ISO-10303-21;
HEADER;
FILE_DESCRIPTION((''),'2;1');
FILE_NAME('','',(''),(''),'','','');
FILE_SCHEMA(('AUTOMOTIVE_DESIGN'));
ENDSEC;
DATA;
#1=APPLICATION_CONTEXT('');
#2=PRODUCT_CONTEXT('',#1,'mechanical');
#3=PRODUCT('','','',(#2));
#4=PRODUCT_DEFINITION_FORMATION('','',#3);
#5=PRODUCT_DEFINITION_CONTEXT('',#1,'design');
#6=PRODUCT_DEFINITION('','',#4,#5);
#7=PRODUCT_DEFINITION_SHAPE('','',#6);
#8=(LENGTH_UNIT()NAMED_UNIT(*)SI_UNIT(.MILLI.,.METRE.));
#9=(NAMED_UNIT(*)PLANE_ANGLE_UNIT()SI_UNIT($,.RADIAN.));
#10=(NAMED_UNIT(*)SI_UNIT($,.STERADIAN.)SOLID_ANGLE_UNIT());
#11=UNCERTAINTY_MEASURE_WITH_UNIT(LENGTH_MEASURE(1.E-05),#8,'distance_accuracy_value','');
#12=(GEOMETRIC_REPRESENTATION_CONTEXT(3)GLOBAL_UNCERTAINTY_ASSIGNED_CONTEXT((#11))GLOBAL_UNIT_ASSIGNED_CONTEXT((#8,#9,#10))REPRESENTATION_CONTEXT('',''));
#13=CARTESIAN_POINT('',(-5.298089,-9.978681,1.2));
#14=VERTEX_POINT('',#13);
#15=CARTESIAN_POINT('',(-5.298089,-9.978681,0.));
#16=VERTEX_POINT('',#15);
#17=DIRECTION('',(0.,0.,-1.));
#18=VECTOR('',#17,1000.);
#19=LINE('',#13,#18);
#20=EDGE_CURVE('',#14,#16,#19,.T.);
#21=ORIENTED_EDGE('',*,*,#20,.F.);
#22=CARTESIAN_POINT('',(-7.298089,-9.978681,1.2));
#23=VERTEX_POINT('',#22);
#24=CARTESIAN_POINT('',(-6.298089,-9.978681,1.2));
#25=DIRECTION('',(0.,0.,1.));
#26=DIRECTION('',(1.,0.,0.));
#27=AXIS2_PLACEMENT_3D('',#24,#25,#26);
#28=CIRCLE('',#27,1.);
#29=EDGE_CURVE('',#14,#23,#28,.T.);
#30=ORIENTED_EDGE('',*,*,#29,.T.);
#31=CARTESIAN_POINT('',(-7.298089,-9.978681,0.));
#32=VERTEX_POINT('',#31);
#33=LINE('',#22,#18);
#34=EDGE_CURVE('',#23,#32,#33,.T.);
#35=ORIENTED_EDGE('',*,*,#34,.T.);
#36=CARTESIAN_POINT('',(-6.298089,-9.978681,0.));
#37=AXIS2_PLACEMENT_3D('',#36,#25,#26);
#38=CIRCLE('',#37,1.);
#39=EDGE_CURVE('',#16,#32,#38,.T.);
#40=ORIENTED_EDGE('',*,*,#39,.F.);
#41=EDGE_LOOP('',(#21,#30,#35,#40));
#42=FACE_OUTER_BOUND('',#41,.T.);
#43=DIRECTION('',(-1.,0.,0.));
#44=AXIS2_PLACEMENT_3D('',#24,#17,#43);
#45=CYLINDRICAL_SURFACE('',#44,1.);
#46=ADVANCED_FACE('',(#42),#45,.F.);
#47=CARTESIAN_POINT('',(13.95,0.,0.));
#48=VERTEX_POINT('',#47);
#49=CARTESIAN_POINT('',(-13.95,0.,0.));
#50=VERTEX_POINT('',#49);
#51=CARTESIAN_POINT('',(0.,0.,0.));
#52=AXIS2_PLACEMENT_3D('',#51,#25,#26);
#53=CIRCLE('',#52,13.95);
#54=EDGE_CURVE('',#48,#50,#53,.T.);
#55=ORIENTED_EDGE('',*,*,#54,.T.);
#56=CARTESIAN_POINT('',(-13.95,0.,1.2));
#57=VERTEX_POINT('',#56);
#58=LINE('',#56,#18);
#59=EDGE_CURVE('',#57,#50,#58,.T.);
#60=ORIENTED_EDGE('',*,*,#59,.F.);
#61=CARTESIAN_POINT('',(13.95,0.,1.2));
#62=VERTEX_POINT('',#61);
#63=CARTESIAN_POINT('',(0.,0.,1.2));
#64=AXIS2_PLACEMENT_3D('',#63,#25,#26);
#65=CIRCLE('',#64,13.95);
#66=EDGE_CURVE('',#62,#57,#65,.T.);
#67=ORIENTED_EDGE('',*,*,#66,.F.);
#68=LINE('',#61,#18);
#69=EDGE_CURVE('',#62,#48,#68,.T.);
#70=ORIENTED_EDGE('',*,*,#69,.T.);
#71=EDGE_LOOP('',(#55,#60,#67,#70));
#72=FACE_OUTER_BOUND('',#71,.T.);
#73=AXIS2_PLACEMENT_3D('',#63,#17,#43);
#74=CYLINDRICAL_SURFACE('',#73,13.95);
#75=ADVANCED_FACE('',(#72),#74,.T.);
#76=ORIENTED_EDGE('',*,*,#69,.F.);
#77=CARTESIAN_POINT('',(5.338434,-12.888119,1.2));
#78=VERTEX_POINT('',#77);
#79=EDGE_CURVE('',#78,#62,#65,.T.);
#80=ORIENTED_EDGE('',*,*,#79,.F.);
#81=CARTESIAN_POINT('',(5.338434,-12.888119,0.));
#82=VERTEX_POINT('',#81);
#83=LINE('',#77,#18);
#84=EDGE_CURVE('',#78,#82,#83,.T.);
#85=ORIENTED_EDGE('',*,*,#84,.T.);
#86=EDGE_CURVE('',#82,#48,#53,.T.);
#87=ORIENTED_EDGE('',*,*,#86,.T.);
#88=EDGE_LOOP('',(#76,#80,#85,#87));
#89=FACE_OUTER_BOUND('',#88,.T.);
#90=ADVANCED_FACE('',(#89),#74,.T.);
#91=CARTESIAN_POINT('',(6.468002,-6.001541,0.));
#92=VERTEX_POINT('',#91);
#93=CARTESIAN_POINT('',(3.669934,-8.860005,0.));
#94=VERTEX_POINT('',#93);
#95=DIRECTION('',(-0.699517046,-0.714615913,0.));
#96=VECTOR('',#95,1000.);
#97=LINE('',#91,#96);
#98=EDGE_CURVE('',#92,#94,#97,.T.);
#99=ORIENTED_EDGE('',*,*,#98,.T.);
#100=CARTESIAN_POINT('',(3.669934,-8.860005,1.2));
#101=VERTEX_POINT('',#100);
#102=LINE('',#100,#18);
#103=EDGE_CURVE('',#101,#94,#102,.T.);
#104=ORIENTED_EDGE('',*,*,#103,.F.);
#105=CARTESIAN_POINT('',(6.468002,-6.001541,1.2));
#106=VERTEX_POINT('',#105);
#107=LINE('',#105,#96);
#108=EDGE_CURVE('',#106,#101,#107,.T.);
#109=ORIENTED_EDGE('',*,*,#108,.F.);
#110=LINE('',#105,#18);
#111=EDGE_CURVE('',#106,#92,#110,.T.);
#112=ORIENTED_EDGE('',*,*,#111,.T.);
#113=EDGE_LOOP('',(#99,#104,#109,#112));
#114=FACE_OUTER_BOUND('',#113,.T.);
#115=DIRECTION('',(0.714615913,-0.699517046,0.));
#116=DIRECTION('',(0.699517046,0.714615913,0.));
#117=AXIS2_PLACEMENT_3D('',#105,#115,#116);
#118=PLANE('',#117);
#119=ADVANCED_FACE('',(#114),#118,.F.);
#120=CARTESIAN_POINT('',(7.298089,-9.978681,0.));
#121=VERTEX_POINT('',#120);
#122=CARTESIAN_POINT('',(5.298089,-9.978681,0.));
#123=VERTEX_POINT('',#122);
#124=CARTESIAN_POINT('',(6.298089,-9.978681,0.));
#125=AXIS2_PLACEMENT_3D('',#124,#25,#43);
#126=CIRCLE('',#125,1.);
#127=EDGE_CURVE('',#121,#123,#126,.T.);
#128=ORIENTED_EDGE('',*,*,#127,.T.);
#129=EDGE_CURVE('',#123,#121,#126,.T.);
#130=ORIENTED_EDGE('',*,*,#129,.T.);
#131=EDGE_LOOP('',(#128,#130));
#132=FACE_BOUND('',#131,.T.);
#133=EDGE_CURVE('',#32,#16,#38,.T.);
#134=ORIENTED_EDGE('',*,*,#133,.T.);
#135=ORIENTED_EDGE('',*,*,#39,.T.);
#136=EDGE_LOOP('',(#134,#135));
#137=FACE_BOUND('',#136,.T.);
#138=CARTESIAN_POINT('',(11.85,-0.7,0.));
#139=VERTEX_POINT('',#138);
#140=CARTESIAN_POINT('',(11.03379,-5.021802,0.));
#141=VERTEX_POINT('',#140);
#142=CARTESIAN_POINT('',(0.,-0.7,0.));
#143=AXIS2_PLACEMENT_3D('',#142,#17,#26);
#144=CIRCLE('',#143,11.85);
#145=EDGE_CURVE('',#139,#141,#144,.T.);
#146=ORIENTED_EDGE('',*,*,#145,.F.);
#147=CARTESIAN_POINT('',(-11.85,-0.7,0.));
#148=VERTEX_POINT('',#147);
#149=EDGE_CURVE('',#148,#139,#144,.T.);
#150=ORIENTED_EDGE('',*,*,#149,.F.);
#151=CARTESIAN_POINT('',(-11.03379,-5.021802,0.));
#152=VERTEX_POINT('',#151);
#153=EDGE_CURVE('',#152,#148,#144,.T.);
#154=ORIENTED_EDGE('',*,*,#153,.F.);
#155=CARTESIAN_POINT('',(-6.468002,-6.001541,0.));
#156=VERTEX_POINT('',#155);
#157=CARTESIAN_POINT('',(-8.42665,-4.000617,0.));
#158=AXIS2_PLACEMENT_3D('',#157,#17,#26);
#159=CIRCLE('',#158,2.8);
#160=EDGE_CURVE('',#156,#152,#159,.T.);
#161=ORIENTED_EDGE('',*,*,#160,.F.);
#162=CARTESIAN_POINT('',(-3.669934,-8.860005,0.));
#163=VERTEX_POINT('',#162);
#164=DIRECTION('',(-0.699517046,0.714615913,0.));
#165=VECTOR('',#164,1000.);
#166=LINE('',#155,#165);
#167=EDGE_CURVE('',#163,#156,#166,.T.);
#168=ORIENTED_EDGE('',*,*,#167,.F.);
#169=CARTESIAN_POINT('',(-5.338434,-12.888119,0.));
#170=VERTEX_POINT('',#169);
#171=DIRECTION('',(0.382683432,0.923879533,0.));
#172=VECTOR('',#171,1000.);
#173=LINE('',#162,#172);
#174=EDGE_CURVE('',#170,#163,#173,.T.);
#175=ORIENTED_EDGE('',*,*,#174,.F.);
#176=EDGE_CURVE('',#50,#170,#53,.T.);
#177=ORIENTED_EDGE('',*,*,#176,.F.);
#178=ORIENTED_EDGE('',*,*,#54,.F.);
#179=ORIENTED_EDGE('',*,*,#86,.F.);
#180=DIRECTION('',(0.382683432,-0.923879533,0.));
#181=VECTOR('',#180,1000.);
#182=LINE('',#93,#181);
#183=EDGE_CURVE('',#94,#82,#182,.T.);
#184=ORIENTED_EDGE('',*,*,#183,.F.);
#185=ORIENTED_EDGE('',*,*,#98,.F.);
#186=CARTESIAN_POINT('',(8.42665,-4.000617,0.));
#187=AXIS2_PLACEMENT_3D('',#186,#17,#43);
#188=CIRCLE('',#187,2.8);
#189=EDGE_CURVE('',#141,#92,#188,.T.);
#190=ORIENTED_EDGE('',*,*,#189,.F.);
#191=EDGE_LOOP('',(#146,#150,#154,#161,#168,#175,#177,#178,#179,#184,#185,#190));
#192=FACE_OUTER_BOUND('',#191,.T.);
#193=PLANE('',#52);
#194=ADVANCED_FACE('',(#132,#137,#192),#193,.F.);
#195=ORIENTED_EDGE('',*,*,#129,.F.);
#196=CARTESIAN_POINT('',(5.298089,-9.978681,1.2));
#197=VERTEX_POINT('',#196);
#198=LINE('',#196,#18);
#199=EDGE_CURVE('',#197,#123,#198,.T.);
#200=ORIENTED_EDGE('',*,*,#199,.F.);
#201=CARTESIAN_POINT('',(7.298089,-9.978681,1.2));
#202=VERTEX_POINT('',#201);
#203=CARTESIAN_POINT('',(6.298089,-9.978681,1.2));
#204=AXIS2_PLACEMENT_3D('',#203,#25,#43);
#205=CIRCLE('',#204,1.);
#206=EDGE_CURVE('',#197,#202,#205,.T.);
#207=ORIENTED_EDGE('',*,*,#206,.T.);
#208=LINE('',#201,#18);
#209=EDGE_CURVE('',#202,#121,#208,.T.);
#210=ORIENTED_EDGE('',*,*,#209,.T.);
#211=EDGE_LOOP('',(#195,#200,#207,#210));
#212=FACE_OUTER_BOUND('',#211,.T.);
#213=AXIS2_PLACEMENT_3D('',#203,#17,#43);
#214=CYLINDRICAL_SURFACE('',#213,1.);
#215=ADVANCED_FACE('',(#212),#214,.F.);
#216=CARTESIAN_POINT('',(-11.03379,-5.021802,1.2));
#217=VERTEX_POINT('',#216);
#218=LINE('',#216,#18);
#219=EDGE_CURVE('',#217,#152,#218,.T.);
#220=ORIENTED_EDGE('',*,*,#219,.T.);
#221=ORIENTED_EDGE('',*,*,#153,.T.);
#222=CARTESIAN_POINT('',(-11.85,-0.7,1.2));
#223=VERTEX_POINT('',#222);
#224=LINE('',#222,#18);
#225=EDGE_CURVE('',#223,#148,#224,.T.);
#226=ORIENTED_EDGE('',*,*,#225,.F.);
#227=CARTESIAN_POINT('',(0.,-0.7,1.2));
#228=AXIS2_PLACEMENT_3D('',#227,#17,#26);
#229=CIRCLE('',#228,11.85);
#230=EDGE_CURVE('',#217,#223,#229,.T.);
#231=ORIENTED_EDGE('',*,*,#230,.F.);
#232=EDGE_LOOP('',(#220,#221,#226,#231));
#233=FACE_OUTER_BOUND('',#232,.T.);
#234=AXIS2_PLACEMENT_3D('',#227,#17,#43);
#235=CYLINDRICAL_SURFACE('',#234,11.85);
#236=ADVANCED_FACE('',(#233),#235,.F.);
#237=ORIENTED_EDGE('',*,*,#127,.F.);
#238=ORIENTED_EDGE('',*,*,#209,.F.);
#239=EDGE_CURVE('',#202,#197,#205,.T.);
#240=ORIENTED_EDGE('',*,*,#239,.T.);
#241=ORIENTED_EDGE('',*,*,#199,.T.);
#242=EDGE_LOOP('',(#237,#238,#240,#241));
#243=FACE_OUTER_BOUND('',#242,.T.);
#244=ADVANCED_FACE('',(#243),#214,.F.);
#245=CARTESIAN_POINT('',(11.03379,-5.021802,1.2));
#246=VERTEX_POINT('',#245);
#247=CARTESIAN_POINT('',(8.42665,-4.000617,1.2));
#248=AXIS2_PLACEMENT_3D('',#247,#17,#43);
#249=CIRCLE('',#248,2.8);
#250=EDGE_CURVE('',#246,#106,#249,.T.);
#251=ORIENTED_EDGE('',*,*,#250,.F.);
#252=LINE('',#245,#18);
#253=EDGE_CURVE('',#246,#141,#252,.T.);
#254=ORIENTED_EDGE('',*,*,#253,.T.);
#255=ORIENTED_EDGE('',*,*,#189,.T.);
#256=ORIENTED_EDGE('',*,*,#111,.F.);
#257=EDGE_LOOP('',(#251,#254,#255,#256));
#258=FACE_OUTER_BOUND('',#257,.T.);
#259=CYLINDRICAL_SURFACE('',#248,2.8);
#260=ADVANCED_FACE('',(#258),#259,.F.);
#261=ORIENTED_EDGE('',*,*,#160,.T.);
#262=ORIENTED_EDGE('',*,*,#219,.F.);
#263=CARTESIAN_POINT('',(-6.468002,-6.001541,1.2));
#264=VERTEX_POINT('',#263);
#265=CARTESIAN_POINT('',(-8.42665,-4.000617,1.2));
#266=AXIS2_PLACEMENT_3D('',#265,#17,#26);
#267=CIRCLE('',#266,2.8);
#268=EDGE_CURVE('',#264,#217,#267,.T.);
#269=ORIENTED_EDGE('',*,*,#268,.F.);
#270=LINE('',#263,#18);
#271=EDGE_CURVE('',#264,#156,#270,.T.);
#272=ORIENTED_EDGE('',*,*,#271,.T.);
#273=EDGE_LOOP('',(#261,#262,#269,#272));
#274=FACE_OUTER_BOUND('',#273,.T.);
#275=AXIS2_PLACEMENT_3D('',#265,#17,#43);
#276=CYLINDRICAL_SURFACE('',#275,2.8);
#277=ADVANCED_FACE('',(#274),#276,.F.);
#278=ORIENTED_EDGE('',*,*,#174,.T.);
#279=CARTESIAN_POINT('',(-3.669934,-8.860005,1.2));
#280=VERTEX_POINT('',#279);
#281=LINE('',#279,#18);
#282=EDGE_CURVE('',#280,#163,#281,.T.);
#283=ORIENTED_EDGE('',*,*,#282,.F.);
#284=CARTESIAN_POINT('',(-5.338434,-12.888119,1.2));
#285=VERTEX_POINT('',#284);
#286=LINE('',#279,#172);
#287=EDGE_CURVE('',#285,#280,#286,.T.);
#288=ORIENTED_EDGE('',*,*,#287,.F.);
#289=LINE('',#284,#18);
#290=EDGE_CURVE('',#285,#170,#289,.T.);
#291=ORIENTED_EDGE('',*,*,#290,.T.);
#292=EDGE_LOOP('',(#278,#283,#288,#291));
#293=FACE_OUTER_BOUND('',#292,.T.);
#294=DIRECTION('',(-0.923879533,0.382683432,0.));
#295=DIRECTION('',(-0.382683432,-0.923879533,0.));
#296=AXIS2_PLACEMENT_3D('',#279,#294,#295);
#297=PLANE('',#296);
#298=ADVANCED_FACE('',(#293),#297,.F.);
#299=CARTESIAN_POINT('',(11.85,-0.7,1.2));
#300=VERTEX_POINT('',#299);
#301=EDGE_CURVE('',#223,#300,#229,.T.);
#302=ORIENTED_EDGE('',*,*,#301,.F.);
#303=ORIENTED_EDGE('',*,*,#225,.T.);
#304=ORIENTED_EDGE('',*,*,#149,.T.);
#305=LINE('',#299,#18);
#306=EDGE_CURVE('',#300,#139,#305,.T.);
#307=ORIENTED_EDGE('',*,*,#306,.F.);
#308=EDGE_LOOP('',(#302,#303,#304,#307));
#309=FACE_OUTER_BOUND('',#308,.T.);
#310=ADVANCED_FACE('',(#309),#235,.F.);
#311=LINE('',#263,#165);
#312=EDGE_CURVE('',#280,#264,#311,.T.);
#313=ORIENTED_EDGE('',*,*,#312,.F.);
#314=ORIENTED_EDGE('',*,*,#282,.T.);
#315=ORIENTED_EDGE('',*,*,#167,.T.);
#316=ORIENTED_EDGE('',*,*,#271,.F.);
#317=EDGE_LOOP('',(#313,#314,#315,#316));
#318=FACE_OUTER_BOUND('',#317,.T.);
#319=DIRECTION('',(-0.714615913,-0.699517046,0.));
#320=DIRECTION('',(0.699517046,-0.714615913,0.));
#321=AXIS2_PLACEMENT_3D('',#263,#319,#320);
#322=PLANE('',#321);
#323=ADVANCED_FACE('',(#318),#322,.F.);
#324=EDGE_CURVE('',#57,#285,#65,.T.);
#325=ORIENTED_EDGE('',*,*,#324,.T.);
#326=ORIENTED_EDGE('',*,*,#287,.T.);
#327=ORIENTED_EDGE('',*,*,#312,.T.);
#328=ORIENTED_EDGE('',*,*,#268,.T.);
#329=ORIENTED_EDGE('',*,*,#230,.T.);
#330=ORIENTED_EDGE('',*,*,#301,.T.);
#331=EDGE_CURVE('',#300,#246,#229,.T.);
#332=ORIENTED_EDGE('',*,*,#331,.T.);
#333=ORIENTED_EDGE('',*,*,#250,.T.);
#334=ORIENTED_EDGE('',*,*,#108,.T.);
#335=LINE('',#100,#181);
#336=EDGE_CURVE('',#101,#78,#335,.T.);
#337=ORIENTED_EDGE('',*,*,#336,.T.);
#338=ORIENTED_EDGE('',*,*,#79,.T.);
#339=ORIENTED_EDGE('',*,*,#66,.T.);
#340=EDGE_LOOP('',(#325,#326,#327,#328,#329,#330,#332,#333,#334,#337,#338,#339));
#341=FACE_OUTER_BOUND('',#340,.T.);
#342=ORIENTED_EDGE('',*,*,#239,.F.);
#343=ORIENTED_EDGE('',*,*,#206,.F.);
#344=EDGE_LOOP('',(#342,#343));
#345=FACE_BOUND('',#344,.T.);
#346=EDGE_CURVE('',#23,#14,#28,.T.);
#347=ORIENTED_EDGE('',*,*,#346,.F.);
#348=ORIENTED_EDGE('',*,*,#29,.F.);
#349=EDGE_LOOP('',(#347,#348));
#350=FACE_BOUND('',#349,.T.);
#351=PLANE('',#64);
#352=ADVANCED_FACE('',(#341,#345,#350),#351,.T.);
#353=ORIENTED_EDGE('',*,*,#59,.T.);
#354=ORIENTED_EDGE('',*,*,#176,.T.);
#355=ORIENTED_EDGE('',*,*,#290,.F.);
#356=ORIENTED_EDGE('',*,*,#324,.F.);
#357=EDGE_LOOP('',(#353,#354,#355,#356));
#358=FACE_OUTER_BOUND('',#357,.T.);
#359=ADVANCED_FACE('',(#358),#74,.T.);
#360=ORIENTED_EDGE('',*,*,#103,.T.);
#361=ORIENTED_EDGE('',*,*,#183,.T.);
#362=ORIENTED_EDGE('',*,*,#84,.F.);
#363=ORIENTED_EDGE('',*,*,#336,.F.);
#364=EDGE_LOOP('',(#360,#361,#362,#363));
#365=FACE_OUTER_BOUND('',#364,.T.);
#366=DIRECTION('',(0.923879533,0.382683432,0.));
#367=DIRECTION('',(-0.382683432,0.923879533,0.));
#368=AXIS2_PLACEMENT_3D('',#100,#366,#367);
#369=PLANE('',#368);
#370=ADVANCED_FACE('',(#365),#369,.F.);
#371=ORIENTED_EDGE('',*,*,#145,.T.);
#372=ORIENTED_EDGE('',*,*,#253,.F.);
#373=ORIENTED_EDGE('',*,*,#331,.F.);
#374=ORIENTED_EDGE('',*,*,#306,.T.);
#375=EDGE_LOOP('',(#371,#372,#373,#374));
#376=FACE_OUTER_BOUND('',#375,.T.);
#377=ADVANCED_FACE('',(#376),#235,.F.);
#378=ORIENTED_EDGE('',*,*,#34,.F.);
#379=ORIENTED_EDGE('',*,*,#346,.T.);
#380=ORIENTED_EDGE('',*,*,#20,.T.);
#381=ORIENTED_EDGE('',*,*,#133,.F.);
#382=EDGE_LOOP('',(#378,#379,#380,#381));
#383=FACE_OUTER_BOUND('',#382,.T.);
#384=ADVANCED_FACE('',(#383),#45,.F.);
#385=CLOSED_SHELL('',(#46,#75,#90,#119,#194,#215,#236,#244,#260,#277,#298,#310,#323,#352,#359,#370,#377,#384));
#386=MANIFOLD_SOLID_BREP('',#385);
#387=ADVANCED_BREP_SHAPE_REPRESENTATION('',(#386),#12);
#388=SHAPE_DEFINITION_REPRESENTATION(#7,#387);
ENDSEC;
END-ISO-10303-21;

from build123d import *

# Parameters (mm, degrees)
SKETCH_1_R        = 1
EXTRUDE_952_DEPTH = 1.2


with BuildPart() as part:
    # 草图1 → Extrude 952 (new body)
    with BuildSketch(Plane.XY):
        with BuildLine():
            Line((-6.468002299, -6.001541065), (-3.669934116, -8.860004717))
            Line((-3.669934116, -8.860004717), (-5.338433881, -12.888119479))
            ThreePointArc((-5.338433881, -12.888119479), (0, 13.95), (5.338433881, -12.888119479))
            Line((5.338433881, -12.888119479), (3.669934116, -8.860004717))
            Line((3.669934116, -8.860004717), (6.468002299, -6.001541065))
            ThreePointArc((6.468002299, -6.001541065), (9.014108926, -6.738296556), (11.033790366, -5.021801727))
            ThreePointArc((11.033790366, -5.021801727), (0, 11.15), (-11.033790366, -5.021801727))
            ThreePointArc((-11.033790366, -5.021801727), (-9.014108926, -6.738296556), (-6.468002299, -6.001541065))
        make_face()
        with Locations((-6.298089329, -9.978680815)):
            Circle(SKETCH_1_R, mode=Mode.SUBTRACT)
        with Locations(Location((6.298089329, -9.978680815, 0), (0, 0, 180))):
            Circle(SKETCH_1_R, mode=Mode.SUBTRACT)
    extrude(amount=EXTRUDE_952_DEPTH)


solid = part.part
